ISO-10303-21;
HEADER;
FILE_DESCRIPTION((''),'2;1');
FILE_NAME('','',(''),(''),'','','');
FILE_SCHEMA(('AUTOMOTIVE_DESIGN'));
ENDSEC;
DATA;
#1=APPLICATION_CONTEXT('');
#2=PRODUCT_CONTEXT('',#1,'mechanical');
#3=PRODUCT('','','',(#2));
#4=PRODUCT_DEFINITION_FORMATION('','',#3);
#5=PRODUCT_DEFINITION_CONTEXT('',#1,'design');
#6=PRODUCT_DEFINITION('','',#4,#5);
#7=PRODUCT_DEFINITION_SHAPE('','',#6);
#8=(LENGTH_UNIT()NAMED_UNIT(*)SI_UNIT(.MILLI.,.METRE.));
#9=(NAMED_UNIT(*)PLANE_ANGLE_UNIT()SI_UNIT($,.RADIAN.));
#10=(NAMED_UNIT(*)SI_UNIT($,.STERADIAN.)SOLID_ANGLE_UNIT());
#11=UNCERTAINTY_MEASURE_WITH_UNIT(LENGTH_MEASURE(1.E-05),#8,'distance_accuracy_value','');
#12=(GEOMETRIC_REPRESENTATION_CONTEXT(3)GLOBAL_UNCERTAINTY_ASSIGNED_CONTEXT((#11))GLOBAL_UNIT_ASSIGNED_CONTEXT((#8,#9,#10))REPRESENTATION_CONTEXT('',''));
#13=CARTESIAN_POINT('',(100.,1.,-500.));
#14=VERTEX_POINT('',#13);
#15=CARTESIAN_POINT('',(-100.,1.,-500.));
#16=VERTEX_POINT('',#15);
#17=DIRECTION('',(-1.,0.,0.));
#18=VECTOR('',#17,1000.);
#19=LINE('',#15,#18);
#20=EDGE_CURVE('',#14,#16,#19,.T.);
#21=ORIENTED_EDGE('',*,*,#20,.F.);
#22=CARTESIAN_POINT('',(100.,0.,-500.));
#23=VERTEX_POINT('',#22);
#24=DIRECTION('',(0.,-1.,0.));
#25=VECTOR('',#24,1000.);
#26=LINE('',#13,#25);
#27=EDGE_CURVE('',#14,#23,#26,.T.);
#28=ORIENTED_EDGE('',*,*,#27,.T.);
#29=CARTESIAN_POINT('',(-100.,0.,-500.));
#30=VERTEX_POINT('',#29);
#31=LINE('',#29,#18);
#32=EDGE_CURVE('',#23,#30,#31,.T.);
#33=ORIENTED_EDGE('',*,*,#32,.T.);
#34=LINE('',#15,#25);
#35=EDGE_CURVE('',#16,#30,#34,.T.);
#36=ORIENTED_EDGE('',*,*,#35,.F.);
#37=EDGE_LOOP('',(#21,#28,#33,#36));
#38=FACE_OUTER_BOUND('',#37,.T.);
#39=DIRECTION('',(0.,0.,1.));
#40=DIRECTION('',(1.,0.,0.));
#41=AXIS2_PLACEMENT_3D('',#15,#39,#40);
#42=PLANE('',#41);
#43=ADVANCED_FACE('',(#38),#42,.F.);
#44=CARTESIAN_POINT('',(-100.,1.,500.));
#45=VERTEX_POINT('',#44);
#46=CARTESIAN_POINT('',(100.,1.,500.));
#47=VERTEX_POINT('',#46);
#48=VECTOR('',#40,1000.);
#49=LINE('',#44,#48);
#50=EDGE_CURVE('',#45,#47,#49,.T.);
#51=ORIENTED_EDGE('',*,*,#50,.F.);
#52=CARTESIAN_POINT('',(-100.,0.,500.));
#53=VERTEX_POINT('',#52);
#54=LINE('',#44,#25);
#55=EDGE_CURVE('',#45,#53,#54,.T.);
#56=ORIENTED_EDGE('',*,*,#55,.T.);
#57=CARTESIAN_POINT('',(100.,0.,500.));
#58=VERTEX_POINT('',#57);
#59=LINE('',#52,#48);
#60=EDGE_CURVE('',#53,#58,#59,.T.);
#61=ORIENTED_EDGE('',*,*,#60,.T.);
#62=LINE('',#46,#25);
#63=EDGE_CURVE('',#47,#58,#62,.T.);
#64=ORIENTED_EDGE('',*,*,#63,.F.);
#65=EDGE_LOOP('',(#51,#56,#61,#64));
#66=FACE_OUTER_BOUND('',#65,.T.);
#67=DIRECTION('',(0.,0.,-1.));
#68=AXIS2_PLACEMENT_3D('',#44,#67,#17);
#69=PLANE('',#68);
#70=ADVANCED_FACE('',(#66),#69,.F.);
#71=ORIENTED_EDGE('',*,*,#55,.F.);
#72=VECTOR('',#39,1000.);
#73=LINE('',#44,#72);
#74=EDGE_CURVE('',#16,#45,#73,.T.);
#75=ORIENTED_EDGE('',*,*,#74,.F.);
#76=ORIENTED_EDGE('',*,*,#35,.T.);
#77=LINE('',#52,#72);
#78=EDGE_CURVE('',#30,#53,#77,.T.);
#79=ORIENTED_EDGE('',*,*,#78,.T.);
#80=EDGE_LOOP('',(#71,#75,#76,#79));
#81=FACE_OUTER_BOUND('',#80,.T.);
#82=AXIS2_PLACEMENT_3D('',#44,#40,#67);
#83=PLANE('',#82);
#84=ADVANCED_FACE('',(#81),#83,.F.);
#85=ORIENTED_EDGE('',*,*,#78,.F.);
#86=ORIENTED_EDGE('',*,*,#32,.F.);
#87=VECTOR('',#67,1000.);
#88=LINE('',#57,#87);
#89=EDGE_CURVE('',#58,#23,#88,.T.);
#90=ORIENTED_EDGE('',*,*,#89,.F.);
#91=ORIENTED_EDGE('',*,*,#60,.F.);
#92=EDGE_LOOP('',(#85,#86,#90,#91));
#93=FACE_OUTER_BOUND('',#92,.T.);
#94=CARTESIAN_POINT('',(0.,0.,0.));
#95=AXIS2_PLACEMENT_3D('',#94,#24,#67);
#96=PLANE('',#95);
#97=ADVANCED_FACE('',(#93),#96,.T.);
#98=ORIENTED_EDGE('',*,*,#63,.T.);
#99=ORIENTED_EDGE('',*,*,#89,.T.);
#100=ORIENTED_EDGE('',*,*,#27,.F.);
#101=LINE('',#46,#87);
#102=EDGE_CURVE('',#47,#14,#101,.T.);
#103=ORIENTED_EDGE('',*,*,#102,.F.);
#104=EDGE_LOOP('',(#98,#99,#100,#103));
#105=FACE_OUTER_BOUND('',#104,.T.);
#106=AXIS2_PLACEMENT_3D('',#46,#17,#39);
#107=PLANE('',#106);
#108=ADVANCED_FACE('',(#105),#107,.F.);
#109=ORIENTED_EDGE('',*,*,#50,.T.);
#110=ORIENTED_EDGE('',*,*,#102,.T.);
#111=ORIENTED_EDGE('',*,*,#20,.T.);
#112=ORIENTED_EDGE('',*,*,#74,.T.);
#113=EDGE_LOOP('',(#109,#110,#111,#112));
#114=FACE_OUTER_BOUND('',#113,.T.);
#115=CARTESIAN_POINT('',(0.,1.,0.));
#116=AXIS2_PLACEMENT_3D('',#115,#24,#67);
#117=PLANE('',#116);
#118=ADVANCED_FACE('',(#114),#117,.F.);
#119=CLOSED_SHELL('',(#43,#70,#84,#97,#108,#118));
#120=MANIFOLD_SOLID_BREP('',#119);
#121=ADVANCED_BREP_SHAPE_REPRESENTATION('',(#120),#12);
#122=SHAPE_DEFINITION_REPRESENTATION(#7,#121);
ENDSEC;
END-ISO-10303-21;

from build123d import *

# Parameters (mm, degrees)
SKETCH1_W           = 200
SKETCH1_H           = 1000
BOSS_EXTRUDE1_DEPTH = 1


with BuildPart() as part:
    # Sketch1 → Boss-Extrude1 (new body)
    with BuildSketch(Plane(origin=(0, 0, 0), x_dir=(1, 0, 0), z_dir=(0, 1, 0))):
        Rectangle(SKETCH1_W, SKETCH1_H)
    extrude(amount=BOSS_EXTRUDE1_DEPTH)


solid = part.part
